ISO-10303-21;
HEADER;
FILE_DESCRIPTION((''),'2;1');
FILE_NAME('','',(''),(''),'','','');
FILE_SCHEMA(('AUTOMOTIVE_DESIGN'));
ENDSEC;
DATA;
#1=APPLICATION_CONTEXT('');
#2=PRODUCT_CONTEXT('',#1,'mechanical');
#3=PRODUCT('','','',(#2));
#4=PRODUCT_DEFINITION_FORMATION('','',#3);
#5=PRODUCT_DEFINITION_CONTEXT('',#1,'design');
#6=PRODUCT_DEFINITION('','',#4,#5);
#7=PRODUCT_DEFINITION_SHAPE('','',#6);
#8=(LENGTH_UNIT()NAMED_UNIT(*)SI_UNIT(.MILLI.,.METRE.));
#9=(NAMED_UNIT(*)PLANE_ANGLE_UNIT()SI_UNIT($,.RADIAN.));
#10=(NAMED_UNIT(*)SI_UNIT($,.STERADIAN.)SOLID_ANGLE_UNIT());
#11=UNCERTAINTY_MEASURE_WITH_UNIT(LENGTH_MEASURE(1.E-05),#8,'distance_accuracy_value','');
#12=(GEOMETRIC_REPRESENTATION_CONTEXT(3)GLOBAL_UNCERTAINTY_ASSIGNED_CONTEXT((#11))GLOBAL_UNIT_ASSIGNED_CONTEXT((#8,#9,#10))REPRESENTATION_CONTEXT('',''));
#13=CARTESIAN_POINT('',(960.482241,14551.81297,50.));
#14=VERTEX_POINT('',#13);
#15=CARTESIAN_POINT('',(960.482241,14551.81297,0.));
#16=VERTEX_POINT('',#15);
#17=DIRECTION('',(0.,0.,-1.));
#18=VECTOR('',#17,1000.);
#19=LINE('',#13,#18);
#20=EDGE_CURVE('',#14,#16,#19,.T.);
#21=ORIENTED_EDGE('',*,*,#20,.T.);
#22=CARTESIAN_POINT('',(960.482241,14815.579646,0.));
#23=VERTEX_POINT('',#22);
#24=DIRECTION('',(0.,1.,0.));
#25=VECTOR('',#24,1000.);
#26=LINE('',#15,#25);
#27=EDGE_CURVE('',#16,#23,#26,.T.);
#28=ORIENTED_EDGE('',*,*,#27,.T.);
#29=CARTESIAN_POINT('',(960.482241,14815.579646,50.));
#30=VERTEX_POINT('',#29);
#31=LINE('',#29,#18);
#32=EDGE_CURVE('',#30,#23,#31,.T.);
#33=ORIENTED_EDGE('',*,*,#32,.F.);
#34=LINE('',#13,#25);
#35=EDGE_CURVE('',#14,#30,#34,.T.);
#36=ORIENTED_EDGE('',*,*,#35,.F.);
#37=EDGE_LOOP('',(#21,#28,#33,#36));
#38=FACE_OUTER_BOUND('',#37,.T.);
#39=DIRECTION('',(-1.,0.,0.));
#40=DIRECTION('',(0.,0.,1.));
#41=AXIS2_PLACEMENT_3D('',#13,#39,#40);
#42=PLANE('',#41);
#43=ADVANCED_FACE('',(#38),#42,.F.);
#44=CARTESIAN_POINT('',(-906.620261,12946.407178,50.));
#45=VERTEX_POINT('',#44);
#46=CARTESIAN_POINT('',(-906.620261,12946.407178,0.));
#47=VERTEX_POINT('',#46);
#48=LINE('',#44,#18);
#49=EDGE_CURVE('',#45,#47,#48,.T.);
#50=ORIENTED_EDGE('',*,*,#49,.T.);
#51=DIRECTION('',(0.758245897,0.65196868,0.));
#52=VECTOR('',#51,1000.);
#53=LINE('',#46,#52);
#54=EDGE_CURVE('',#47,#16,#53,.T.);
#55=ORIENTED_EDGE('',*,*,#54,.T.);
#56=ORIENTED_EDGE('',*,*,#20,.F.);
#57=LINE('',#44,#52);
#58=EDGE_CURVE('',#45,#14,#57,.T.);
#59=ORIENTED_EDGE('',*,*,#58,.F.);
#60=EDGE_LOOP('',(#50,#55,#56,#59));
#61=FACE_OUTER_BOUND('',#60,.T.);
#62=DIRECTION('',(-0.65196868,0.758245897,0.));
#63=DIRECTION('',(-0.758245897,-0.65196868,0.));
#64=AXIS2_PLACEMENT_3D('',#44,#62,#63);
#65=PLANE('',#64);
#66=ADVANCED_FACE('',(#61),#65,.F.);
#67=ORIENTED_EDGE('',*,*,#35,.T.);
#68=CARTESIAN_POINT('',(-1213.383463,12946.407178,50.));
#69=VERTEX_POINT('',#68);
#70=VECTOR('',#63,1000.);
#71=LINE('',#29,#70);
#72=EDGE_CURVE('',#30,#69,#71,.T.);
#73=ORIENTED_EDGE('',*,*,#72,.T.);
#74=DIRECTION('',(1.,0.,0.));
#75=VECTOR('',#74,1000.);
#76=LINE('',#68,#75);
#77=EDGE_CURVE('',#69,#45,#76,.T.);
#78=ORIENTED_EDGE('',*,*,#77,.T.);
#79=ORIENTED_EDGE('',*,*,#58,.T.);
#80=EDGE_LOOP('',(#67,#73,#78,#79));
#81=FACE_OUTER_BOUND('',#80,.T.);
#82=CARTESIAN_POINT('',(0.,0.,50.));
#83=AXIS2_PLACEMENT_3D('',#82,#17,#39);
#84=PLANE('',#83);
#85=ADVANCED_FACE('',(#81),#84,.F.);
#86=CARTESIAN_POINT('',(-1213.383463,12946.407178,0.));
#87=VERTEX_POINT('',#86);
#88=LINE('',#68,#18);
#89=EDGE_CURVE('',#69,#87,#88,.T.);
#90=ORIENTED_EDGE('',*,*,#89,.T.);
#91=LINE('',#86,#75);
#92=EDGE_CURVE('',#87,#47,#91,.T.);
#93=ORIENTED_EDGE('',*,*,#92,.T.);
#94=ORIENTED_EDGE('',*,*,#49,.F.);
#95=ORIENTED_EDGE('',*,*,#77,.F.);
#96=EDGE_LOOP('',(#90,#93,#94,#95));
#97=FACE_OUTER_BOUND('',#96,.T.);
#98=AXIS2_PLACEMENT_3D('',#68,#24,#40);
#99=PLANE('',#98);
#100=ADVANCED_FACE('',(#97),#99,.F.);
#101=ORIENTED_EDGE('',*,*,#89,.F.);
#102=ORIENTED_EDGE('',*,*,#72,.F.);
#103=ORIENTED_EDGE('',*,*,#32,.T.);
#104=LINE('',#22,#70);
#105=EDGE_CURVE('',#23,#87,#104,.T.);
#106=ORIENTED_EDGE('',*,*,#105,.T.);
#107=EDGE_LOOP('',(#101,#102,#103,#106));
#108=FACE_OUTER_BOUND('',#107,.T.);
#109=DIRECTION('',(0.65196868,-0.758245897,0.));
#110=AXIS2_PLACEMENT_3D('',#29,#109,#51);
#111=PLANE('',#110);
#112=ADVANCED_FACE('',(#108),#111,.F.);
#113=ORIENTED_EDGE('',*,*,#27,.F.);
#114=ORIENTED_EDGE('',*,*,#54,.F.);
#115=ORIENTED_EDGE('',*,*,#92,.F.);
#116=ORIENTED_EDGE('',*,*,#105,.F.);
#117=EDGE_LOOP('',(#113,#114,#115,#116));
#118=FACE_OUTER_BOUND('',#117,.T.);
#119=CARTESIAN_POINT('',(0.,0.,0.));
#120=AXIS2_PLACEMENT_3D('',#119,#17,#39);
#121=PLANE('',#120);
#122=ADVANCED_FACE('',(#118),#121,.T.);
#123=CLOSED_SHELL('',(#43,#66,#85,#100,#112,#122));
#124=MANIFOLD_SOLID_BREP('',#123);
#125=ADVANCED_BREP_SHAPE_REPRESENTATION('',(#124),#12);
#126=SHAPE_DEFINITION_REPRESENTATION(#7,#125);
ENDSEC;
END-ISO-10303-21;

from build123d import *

# Parameters (mm, degrees)
BOSS_EXTRUDE1_DEPTH = 50


with BuildPart() as part:
    # Sketch1 → Boss-Extrude1 (new body)
    with BuildSketch(Plane.XY):
        Polygon((-1213.383462756, 12946.407177591), (-906.620260802, 12946.407177591), (960.48224113, 14551.812970124), (960.48224113, 14815.579646482), align=None)
    extrude(amount=BOSS_EXTRUDE1_DEPTH)


solid = part.part
